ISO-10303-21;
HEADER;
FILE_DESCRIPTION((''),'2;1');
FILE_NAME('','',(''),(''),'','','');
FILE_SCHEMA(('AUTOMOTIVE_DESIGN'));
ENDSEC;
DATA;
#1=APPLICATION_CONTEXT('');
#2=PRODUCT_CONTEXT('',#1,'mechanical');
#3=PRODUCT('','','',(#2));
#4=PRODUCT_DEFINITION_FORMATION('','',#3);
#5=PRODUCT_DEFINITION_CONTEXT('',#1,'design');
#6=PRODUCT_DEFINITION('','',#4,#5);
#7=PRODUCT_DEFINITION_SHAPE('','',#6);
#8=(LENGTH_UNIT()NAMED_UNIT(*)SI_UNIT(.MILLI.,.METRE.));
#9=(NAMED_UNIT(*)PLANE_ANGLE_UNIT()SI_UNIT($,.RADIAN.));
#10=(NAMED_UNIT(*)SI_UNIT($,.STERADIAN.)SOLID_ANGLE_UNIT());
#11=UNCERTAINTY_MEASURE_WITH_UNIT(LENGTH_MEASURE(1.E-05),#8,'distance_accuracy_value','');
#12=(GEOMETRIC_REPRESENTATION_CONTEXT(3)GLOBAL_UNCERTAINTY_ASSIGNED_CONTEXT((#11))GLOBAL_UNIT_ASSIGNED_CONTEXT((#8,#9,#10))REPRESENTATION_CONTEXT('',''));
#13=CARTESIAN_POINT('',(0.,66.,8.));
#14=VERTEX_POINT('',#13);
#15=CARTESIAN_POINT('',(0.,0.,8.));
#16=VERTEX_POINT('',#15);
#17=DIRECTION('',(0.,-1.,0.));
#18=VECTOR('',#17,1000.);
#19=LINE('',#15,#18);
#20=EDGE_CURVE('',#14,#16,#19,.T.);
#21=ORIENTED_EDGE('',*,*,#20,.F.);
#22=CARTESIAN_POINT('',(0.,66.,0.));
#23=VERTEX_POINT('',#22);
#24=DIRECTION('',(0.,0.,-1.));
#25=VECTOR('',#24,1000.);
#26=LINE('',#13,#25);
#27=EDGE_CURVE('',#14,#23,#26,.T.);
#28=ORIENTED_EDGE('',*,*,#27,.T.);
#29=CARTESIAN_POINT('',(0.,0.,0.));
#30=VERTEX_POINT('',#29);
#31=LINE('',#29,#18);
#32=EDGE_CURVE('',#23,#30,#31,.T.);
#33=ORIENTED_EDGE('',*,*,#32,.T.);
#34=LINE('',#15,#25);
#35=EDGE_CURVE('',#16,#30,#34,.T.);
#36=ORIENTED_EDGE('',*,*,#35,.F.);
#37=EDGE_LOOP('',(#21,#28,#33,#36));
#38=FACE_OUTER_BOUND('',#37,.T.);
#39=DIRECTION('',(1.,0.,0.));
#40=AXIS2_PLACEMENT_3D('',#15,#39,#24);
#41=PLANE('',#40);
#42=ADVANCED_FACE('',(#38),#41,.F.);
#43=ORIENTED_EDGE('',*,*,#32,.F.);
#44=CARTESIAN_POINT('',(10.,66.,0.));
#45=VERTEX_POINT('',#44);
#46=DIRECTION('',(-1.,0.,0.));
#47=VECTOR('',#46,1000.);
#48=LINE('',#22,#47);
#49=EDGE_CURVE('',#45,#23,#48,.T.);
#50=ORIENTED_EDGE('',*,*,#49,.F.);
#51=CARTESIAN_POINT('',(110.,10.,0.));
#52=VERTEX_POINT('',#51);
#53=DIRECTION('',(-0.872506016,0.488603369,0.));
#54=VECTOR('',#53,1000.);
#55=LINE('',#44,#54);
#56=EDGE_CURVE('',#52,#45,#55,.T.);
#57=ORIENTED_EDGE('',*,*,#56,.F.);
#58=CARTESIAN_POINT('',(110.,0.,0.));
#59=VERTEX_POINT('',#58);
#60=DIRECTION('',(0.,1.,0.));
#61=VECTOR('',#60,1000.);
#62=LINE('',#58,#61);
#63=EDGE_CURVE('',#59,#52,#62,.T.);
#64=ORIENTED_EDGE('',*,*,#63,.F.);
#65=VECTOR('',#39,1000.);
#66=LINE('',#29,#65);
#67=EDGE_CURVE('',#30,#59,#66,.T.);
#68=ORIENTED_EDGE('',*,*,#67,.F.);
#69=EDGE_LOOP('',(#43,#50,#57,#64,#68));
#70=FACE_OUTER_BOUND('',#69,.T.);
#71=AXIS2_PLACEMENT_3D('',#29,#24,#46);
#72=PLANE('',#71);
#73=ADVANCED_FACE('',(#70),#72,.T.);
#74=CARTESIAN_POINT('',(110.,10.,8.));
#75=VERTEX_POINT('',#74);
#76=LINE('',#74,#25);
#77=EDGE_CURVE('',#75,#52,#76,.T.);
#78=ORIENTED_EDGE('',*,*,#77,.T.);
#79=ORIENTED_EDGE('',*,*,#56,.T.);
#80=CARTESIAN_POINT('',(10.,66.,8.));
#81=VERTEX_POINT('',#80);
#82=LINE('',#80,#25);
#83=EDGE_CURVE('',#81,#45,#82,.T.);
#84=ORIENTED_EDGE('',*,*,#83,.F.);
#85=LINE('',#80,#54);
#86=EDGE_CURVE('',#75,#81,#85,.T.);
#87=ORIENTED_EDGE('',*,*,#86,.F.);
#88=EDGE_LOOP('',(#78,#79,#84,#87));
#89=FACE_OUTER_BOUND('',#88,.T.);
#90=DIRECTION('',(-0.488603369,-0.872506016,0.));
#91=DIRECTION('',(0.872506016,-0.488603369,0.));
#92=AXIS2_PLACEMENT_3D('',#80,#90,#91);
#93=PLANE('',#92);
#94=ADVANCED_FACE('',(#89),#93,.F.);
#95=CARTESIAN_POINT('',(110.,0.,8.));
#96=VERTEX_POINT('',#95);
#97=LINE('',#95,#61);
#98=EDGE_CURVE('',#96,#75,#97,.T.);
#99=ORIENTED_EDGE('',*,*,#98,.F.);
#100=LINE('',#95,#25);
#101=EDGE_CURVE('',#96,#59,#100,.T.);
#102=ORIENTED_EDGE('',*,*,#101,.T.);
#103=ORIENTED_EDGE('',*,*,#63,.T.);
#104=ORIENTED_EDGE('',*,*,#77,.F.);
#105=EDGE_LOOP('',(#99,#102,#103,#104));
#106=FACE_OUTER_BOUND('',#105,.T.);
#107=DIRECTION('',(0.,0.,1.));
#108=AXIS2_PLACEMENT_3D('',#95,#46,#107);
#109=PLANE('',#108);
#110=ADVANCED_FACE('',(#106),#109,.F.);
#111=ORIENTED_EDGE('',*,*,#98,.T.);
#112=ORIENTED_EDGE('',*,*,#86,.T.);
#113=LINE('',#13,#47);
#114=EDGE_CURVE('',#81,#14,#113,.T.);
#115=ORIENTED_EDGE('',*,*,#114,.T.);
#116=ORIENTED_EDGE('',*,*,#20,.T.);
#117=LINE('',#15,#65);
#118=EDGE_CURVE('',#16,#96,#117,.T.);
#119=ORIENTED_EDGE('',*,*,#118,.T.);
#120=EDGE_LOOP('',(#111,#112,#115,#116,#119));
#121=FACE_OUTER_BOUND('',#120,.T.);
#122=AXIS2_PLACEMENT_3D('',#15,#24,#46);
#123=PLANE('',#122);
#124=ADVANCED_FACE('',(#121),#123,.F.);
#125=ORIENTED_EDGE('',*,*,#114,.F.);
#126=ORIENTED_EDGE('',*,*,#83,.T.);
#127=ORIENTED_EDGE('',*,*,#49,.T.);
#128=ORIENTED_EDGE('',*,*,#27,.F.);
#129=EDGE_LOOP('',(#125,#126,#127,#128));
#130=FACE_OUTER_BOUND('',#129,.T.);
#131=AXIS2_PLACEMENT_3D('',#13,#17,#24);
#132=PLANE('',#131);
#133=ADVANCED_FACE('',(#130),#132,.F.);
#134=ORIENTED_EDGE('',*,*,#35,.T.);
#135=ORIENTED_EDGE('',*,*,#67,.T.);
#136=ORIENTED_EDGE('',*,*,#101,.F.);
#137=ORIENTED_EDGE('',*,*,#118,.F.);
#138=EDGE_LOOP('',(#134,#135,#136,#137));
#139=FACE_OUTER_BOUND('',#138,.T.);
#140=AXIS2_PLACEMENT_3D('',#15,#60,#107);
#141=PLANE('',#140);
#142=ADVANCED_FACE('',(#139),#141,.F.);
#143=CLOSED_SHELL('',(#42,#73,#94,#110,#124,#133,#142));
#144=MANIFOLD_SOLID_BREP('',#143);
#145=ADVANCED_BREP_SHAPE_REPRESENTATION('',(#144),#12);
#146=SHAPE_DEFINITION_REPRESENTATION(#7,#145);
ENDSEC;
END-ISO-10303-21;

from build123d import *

# Parameters (mm, degrees)
BOSS_EXTRUDE1_DEPTH = 8


with BuildPart() as part:
    # Sketch1 → Boss-Extrude1 (new body)
    with BuildSketch(Plane.XY):
        Polygon((10, 66), (110, 10), (110, 0), (0, 0), (0, 66), align=None)
    extrude(amount=BOSS_EXTRUDE1_DEPTH)


solid = part.part
